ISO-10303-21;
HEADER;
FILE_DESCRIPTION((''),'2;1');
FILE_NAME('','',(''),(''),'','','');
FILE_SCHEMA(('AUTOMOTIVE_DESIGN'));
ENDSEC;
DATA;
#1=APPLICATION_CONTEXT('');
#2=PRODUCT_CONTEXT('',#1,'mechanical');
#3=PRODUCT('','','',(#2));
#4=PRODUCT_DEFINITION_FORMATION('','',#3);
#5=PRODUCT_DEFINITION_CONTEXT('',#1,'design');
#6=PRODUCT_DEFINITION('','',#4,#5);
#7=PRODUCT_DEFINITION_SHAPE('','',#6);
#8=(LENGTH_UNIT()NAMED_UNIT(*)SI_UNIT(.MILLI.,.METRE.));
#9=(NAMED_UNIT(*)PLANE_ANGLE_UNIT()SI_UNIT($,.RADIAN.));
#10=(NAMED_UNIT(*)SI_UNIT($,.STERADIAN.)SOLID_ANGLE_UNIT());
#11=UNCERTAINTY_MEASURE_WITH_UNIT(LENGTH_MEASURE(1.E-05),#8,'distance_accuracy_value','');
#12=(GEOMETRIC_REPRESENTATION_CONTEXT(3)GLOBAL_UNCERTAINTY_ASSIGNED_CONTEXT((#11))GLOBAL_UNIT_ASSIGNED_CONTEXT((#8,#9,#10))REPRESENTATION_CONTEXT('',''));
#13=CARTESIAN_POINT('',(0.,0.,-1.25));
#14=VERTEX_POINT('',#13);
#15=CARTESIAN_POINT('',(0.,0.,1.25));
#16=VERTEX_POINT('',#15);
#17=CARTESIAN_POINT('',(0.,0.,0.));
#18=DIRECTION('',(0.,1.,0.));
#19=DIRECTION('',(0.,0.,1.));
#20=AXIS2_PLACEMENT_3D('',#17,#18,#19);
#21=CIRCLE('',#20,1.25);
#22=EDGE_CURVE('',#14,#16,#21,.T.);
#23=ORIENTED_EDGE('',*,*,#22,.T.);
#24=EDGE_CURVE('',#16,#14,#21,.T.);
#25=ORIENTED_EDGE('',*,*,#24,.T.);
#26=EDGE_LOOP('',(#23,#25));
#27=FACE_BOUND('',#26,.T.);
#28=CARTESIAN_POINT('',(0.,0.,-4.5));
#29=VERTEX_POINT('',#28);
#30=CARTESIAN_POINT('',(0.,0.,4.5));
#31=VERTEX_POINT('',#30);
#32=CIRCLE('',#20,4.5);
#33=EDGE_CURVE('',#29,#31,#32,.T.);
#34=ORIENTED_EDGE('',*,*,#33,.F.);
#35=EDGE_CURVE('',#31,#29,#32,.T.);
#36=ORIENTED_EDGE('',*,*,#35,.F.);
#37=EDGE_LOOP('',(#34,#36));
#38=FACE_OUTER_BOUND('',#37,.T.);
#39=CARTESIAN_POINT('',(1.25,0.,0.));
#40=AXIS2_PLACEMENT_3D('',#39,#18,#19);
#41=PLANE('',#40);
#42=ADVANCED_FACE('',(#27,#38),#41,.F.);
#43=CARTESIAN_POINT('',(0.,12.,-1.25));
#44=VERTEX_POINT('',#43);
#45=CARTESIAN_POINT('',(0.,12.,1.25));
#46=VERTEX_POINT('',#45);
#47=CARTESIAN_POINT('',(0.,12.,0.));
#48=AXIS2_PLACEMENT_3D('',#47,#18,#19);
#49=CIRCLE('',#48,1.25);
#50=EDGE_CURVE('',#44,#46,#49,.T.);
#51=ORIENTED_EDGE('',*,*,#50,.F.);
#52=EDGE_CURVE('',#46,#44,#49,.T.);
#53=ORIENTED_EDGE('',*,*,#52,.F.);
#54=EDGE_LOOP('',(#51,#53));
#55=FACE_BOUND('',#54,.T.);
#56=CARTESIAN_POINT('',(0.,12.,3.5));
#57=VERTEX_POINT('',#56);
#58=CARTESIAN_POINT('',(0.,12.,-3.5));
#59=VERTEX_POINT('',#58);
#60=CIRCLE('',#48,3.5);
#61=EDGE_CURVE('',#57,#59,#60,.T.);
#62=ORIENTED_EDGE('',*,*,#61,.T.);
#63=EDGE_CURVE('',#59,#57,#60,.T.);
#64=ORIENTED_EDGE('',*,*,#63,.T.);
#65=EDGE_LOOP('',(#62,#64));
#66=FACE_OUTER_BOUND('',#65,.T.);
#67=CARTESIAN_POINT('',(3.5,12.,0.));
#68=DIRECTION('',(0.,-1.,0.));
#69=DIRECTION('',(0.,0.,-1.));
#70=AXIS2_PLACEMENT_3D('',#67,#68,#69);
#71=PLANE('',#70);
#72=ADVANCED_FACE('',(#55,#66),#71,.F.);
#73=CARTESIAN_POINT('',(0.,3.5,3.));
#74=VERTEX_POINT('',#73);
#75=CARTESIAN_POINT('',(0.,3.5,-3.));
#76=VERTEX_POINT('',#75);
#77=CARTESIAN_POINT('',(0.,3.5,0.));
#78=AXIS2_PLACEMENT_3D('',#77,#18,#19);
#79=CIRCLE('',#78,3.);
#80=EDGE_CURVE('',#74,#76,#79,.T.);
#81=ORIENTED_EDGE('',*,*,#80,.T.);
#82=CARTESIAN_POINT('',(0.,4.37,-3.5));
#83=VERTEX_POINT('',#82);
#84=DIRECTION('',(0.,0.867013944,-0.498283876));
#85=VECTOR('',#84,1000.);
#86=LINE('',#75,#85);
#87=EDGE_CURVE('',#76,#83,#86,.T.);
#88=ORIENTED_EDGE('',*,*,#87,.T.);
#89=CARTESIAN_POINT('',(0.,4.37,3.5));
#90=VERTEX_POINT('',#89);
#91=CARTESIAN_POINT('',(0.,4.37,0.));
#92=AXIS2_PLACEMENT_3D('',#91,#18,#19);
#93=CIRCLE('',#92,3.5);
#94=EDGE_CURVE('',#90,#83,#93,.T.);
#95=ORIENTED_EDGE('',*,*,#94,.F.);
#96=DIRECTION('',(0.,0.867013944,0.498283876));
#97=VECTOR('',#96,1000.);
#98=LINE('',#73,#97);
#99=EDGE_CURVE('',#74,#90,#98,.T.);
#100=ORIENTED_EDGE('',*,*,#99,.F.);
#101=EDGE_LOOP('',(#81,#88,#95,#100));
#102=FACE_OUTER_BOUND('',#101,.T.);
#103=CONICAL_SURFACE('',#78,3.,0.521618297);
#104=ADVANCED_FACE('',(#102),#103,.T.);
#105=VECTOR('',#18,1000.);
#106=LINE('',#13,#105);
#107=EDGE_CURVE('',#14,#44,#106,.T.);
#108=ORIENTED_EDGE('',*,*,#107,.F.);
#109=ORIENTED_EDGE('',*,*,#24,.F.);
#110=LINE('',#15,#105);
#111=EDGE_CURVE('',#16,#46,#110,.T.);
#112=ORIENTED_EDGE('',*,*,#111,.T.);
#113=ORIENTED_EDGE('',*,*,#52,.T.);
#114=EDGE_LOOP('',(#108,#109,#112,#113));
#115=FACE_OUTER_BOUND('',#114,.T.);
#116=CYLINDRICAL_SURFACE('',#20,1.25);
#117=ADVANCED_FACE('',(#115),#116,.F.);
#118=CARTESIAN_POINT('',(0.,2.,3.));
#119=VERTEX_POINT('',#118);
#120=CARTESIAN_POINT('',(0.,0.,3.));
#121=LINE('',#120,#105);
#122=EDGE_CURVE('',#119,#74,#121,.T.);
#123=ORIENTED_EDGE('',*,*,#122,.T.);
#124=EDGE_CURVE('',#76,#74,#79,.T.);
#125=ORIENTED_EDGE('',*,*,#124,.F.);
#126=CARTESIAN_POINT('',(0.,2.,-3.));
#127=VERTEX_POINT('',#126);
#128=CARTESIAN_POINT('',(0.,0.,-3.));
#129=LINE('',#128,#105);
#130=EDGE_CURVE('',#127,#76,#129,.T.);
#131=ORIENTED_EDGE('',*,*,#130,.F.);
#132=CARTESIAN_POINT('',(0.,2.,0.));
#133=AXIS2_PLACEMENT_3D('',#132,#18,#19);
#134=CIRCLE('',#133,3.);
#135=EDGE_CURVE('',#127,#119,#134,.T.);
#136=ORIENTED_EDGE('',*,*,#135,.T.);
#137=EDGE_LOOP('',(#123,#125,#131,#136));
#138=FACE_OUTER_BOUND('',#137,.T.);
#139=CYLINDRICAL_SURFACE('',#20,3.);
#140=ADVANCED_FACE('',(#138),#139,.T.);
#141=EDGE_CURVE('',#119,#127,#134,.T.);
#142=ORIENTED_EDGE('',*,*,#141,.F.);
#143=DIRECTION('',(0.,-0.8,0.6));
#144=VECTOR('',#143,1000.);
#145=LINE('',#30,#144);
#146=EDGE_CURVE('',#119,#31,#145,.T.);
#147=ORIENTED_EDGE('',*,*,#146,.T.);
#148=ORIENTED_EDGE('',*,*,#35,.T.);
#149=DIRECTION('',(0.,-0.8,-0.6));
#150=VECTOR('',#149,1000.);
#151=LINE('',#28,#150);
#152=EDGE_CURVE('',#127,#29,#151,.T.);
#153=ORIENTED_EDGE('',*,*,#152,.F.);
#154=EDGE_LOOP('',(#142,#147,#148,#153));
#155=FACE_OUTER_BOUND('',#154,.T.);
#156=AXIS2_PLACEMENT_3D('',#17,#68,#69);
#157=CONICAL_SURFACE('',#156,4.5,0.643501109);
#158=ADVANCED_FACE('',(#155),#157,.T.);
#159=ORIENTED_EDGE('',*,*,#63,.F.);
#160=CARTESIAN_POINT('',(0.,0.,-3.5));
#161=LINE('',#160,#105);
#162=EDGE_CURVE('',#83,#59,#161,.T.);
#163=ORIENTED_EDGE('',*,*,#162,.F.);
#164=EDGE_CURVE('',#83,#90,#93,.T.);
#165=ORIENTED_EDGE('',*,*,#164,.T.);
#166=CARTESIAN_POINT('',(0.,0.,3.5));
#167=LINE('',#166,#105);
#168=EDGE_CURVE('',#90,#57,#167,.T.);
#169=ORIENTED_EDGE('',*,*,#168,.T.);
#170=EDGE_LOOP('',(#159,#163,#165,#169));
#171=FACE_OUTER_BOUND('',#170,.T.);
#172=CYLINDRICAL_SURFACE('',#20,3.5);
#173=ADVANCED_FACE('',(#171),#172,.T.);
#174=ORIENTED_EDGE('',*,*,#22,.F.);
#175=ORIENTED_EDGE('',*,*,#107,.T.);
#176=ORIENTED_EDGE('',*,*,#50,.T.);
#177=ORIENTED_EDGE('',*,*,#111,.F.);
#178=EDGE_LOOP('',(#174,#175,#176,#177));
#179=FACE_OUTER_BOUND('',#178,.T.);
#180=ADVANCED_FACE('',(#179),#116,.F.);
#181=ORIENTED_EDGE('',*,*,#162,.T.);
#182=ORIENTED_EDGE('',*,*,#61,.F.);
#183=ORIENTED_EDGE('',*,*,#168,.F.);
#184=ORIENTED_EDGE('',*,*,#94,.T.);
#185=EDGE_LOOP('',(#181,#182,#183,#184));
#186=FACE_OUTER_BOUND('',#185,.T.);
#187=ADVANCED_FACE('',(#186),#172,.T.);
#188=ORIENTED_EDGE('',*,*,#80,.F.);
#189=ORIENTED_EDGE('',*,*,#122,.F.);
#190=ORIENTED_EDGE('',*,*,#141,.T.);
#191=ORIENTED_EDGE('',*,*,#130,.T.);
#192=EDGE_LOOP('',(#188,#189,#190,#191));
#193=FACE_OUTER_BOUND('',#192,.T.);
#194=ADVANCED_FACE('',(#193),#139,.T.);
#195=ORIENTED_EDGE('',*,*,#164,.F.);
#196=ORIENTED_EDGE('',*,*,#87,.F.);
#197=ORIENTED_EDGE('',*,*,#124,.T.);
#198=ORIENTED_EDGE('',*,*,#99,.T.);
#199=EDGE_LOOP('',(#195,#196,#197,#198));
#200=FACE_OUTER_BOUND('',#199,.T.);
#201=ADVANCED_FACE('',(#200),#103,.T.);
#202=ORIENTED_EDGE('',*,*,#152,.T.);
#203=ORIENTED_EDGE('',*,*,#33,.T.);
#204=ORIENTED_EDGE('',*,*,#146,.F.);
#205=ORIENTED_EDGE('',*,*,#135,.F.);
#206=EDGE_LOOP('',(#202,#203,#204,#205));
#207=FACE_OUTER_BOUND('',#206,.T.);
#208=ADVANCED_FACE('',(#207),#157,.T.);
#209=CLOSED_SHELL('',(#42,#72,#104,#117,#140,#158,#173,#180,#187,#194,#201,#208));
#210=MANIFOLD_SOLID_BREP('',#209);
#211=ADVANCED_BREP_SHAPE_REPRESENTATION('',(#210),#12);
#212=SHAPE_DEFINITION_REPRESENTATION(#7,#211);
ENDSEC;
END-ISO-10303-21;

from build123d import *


with BuildPart() as part:
    # 草图1 → 旋转1 (revolve)
    with BuildSketch(Plane.XY, mode=Mode.PRIVATE) as revolve_1_sk:
        Polygon((1.25, 0), (4.5, 0), (3, 2), (3, 3.5), (3.5, 4.37), (3.5, 12), (1.25, 12), align=None)
    revolve(revolve_1_sk.sketch.rotate(Axis((0, 0, 0), (0, 1, 0)), 270), axis=Axis((0, 0, 0), (0, 1, 0)))


solid = part.part
